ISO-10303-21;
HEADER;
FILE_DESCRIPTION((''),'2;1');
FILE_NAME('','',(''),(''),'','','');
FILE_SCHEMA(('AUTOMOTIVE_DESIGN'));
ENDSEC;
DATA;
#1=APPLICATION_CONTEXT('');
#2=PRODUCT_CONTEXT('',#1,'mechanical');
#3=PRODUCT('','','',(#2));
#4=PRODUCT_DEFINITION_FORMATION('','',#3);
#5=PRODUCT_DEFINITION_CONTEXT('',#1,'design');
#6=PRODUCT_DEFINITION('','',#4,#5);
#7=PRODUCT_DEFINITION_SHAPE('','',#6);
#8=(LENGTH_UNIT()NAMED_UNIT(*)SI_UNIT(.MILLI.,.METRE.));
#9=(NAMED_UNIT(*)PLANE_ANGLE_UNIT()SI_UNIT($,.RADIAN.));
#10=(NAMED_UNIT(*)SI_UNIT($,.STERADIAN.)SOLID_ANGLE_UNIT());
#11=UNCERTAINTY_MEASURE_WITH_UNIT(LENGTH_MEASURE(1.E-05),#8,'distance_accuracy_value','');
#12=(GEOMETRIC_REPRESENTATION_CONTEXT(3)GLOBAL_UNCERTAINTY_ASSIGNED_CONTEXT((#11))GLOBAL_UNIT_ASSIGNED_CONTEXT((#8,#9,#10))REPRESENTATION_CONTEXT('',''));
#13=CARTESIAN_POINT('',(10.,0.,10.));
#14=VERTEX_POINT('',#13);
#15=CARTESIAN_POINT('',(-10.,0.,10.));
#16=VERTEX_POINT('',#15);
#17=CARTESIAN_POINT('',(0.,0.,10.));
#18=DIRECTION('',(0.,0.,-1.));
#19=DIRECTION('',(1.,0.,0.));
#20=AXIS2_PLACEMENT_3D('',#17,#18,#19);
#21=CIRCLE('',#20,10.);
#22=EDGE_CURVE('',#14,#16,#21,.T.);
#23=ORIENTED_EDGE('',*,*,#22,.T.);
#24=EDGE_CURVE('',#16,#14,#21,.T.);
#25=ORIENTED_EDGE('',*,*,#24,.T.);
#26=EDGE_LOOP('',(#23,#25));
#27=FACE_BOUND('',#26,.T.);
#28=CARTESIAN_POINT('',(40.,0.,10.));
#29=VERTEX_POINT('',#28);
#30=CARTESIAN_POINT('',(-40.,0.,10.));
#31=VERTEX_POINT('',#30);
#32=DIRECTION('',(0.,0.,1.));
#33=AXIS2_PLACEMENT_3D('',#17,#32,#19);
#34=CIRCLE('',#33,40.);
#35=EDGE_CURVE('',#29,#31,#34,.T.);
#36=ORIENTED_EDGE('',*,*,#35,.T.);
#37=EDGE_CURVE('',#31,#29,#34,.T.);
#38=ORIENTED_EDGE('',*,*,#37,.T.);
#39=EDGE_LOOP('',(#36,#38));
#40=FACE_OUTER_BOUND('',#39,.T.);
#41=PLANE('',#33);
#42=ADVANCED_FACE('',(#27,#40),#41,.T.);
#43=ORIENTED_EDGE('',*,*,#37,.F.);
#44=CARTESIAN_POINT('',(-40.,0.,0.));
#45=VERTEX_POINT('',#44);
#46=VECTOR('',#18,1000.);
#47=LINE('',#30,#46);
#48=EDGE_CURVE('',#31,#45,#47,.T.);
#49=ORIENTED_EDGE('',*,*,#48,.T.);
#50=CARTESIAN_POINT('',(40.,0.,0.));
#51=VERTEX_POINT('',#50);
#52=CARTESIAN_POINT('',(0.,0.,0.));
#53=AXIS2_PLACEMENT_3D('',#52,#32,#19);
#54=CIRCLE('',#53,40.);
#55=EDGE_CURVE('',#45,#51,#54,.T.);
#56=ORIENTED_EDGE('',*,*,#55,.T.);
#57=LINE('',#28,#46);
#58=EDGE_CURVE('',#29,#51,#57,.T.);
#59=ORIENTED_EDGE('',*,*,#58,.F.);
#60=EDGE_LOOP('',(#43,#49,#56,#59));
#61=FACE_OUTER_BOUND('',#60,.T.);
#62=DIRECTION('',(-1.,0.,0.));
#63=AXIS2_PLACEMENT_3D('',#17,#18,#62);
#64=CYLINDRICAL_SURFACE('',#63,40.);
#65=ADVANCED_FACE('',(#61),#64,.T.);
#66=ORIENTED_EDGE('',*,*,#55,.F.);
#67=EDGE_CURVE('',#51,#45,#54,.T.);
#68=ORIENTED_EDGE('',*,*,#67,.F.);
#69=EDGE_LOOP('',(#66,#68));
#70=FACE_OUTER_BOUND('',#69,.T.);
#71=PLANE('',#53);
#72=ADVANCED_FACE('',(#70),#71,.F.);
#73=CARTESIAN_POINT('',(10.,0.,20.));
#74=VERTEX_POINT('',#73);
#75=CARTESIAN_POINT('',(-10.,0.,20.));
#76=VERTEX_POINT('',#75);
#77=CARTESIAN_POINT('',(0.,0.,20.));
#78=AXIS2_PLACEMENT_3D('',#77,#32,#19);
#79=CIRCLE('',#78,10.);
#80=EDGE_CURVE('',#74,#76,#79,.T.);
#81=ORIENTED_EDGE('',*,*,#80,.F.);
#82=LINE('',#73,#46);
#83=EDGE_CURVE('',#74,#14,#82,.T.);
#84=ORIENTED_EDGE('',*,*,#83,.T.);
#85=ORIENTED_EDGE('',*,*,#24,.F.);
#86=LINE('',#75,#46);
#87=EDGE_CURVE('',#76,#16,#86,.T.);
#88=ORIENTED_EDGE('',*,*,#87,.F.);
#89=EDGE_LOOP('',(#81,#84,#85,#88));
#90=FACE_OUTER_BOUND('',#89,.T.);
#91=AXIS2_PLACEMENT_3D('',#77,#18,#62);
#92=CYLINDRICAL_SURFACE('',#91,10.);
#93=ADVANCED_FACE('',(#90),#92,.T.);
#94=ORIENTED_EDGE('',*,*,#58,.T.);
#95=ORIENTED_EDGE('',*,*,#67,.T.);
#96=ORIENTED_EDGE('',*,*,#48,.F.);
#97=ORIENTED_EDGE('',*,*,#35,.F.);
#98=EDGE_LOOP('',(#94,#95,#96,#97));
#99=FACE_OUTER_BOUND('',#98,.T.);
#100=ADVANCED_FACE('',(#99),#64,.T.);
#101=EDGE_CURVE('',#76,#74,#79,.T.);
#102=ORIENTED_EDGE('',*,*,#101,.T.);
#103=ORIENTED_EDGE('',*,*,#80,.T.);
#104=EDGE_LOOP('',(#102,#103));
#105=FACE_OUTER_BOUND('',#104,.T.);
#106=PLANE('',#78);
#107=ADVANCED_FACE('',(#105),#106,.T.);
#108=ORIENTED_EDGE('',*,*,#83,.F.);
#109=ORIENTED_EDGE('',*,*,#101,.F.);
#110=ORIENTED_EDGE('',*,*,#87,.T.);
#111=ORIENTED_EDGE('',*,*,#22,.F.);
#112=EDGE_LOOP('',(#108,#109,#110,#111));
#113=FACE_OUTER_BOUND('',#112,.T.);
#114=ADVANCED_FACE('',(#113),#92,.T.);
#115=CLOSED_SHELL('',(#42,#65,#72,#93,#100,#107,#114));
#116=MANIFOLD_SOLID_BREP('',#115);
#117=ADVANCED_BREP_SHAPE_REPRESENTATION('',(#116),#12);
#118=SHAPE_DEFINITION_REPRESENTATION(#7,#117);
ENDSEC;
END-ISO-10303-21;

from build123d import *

# Parameters (mm, degrees)
SKETCH_1_R      = 40
EXTRUDE_1_DEPTH = 10
SKETCH_2_R      = 10
EXTRUDE_2_DEPTH = 20


with BuildPart() as part:
    # 草图1 → 凸台-拉伸1 (new body)
    with BuildSketch(Plane.XY):
        Circle(SKETCH_1_R)
    extrude(amount=EXTRUDE_1_DEPTH)

    # 草图2 → 凸台-拉伸2 (add)
    with BuildSketch(Plane.XY):
        Circle(SKETCH_2_R)
    extrude(amount=EXTRUDE_2_DEPTH)


solid = part.part
